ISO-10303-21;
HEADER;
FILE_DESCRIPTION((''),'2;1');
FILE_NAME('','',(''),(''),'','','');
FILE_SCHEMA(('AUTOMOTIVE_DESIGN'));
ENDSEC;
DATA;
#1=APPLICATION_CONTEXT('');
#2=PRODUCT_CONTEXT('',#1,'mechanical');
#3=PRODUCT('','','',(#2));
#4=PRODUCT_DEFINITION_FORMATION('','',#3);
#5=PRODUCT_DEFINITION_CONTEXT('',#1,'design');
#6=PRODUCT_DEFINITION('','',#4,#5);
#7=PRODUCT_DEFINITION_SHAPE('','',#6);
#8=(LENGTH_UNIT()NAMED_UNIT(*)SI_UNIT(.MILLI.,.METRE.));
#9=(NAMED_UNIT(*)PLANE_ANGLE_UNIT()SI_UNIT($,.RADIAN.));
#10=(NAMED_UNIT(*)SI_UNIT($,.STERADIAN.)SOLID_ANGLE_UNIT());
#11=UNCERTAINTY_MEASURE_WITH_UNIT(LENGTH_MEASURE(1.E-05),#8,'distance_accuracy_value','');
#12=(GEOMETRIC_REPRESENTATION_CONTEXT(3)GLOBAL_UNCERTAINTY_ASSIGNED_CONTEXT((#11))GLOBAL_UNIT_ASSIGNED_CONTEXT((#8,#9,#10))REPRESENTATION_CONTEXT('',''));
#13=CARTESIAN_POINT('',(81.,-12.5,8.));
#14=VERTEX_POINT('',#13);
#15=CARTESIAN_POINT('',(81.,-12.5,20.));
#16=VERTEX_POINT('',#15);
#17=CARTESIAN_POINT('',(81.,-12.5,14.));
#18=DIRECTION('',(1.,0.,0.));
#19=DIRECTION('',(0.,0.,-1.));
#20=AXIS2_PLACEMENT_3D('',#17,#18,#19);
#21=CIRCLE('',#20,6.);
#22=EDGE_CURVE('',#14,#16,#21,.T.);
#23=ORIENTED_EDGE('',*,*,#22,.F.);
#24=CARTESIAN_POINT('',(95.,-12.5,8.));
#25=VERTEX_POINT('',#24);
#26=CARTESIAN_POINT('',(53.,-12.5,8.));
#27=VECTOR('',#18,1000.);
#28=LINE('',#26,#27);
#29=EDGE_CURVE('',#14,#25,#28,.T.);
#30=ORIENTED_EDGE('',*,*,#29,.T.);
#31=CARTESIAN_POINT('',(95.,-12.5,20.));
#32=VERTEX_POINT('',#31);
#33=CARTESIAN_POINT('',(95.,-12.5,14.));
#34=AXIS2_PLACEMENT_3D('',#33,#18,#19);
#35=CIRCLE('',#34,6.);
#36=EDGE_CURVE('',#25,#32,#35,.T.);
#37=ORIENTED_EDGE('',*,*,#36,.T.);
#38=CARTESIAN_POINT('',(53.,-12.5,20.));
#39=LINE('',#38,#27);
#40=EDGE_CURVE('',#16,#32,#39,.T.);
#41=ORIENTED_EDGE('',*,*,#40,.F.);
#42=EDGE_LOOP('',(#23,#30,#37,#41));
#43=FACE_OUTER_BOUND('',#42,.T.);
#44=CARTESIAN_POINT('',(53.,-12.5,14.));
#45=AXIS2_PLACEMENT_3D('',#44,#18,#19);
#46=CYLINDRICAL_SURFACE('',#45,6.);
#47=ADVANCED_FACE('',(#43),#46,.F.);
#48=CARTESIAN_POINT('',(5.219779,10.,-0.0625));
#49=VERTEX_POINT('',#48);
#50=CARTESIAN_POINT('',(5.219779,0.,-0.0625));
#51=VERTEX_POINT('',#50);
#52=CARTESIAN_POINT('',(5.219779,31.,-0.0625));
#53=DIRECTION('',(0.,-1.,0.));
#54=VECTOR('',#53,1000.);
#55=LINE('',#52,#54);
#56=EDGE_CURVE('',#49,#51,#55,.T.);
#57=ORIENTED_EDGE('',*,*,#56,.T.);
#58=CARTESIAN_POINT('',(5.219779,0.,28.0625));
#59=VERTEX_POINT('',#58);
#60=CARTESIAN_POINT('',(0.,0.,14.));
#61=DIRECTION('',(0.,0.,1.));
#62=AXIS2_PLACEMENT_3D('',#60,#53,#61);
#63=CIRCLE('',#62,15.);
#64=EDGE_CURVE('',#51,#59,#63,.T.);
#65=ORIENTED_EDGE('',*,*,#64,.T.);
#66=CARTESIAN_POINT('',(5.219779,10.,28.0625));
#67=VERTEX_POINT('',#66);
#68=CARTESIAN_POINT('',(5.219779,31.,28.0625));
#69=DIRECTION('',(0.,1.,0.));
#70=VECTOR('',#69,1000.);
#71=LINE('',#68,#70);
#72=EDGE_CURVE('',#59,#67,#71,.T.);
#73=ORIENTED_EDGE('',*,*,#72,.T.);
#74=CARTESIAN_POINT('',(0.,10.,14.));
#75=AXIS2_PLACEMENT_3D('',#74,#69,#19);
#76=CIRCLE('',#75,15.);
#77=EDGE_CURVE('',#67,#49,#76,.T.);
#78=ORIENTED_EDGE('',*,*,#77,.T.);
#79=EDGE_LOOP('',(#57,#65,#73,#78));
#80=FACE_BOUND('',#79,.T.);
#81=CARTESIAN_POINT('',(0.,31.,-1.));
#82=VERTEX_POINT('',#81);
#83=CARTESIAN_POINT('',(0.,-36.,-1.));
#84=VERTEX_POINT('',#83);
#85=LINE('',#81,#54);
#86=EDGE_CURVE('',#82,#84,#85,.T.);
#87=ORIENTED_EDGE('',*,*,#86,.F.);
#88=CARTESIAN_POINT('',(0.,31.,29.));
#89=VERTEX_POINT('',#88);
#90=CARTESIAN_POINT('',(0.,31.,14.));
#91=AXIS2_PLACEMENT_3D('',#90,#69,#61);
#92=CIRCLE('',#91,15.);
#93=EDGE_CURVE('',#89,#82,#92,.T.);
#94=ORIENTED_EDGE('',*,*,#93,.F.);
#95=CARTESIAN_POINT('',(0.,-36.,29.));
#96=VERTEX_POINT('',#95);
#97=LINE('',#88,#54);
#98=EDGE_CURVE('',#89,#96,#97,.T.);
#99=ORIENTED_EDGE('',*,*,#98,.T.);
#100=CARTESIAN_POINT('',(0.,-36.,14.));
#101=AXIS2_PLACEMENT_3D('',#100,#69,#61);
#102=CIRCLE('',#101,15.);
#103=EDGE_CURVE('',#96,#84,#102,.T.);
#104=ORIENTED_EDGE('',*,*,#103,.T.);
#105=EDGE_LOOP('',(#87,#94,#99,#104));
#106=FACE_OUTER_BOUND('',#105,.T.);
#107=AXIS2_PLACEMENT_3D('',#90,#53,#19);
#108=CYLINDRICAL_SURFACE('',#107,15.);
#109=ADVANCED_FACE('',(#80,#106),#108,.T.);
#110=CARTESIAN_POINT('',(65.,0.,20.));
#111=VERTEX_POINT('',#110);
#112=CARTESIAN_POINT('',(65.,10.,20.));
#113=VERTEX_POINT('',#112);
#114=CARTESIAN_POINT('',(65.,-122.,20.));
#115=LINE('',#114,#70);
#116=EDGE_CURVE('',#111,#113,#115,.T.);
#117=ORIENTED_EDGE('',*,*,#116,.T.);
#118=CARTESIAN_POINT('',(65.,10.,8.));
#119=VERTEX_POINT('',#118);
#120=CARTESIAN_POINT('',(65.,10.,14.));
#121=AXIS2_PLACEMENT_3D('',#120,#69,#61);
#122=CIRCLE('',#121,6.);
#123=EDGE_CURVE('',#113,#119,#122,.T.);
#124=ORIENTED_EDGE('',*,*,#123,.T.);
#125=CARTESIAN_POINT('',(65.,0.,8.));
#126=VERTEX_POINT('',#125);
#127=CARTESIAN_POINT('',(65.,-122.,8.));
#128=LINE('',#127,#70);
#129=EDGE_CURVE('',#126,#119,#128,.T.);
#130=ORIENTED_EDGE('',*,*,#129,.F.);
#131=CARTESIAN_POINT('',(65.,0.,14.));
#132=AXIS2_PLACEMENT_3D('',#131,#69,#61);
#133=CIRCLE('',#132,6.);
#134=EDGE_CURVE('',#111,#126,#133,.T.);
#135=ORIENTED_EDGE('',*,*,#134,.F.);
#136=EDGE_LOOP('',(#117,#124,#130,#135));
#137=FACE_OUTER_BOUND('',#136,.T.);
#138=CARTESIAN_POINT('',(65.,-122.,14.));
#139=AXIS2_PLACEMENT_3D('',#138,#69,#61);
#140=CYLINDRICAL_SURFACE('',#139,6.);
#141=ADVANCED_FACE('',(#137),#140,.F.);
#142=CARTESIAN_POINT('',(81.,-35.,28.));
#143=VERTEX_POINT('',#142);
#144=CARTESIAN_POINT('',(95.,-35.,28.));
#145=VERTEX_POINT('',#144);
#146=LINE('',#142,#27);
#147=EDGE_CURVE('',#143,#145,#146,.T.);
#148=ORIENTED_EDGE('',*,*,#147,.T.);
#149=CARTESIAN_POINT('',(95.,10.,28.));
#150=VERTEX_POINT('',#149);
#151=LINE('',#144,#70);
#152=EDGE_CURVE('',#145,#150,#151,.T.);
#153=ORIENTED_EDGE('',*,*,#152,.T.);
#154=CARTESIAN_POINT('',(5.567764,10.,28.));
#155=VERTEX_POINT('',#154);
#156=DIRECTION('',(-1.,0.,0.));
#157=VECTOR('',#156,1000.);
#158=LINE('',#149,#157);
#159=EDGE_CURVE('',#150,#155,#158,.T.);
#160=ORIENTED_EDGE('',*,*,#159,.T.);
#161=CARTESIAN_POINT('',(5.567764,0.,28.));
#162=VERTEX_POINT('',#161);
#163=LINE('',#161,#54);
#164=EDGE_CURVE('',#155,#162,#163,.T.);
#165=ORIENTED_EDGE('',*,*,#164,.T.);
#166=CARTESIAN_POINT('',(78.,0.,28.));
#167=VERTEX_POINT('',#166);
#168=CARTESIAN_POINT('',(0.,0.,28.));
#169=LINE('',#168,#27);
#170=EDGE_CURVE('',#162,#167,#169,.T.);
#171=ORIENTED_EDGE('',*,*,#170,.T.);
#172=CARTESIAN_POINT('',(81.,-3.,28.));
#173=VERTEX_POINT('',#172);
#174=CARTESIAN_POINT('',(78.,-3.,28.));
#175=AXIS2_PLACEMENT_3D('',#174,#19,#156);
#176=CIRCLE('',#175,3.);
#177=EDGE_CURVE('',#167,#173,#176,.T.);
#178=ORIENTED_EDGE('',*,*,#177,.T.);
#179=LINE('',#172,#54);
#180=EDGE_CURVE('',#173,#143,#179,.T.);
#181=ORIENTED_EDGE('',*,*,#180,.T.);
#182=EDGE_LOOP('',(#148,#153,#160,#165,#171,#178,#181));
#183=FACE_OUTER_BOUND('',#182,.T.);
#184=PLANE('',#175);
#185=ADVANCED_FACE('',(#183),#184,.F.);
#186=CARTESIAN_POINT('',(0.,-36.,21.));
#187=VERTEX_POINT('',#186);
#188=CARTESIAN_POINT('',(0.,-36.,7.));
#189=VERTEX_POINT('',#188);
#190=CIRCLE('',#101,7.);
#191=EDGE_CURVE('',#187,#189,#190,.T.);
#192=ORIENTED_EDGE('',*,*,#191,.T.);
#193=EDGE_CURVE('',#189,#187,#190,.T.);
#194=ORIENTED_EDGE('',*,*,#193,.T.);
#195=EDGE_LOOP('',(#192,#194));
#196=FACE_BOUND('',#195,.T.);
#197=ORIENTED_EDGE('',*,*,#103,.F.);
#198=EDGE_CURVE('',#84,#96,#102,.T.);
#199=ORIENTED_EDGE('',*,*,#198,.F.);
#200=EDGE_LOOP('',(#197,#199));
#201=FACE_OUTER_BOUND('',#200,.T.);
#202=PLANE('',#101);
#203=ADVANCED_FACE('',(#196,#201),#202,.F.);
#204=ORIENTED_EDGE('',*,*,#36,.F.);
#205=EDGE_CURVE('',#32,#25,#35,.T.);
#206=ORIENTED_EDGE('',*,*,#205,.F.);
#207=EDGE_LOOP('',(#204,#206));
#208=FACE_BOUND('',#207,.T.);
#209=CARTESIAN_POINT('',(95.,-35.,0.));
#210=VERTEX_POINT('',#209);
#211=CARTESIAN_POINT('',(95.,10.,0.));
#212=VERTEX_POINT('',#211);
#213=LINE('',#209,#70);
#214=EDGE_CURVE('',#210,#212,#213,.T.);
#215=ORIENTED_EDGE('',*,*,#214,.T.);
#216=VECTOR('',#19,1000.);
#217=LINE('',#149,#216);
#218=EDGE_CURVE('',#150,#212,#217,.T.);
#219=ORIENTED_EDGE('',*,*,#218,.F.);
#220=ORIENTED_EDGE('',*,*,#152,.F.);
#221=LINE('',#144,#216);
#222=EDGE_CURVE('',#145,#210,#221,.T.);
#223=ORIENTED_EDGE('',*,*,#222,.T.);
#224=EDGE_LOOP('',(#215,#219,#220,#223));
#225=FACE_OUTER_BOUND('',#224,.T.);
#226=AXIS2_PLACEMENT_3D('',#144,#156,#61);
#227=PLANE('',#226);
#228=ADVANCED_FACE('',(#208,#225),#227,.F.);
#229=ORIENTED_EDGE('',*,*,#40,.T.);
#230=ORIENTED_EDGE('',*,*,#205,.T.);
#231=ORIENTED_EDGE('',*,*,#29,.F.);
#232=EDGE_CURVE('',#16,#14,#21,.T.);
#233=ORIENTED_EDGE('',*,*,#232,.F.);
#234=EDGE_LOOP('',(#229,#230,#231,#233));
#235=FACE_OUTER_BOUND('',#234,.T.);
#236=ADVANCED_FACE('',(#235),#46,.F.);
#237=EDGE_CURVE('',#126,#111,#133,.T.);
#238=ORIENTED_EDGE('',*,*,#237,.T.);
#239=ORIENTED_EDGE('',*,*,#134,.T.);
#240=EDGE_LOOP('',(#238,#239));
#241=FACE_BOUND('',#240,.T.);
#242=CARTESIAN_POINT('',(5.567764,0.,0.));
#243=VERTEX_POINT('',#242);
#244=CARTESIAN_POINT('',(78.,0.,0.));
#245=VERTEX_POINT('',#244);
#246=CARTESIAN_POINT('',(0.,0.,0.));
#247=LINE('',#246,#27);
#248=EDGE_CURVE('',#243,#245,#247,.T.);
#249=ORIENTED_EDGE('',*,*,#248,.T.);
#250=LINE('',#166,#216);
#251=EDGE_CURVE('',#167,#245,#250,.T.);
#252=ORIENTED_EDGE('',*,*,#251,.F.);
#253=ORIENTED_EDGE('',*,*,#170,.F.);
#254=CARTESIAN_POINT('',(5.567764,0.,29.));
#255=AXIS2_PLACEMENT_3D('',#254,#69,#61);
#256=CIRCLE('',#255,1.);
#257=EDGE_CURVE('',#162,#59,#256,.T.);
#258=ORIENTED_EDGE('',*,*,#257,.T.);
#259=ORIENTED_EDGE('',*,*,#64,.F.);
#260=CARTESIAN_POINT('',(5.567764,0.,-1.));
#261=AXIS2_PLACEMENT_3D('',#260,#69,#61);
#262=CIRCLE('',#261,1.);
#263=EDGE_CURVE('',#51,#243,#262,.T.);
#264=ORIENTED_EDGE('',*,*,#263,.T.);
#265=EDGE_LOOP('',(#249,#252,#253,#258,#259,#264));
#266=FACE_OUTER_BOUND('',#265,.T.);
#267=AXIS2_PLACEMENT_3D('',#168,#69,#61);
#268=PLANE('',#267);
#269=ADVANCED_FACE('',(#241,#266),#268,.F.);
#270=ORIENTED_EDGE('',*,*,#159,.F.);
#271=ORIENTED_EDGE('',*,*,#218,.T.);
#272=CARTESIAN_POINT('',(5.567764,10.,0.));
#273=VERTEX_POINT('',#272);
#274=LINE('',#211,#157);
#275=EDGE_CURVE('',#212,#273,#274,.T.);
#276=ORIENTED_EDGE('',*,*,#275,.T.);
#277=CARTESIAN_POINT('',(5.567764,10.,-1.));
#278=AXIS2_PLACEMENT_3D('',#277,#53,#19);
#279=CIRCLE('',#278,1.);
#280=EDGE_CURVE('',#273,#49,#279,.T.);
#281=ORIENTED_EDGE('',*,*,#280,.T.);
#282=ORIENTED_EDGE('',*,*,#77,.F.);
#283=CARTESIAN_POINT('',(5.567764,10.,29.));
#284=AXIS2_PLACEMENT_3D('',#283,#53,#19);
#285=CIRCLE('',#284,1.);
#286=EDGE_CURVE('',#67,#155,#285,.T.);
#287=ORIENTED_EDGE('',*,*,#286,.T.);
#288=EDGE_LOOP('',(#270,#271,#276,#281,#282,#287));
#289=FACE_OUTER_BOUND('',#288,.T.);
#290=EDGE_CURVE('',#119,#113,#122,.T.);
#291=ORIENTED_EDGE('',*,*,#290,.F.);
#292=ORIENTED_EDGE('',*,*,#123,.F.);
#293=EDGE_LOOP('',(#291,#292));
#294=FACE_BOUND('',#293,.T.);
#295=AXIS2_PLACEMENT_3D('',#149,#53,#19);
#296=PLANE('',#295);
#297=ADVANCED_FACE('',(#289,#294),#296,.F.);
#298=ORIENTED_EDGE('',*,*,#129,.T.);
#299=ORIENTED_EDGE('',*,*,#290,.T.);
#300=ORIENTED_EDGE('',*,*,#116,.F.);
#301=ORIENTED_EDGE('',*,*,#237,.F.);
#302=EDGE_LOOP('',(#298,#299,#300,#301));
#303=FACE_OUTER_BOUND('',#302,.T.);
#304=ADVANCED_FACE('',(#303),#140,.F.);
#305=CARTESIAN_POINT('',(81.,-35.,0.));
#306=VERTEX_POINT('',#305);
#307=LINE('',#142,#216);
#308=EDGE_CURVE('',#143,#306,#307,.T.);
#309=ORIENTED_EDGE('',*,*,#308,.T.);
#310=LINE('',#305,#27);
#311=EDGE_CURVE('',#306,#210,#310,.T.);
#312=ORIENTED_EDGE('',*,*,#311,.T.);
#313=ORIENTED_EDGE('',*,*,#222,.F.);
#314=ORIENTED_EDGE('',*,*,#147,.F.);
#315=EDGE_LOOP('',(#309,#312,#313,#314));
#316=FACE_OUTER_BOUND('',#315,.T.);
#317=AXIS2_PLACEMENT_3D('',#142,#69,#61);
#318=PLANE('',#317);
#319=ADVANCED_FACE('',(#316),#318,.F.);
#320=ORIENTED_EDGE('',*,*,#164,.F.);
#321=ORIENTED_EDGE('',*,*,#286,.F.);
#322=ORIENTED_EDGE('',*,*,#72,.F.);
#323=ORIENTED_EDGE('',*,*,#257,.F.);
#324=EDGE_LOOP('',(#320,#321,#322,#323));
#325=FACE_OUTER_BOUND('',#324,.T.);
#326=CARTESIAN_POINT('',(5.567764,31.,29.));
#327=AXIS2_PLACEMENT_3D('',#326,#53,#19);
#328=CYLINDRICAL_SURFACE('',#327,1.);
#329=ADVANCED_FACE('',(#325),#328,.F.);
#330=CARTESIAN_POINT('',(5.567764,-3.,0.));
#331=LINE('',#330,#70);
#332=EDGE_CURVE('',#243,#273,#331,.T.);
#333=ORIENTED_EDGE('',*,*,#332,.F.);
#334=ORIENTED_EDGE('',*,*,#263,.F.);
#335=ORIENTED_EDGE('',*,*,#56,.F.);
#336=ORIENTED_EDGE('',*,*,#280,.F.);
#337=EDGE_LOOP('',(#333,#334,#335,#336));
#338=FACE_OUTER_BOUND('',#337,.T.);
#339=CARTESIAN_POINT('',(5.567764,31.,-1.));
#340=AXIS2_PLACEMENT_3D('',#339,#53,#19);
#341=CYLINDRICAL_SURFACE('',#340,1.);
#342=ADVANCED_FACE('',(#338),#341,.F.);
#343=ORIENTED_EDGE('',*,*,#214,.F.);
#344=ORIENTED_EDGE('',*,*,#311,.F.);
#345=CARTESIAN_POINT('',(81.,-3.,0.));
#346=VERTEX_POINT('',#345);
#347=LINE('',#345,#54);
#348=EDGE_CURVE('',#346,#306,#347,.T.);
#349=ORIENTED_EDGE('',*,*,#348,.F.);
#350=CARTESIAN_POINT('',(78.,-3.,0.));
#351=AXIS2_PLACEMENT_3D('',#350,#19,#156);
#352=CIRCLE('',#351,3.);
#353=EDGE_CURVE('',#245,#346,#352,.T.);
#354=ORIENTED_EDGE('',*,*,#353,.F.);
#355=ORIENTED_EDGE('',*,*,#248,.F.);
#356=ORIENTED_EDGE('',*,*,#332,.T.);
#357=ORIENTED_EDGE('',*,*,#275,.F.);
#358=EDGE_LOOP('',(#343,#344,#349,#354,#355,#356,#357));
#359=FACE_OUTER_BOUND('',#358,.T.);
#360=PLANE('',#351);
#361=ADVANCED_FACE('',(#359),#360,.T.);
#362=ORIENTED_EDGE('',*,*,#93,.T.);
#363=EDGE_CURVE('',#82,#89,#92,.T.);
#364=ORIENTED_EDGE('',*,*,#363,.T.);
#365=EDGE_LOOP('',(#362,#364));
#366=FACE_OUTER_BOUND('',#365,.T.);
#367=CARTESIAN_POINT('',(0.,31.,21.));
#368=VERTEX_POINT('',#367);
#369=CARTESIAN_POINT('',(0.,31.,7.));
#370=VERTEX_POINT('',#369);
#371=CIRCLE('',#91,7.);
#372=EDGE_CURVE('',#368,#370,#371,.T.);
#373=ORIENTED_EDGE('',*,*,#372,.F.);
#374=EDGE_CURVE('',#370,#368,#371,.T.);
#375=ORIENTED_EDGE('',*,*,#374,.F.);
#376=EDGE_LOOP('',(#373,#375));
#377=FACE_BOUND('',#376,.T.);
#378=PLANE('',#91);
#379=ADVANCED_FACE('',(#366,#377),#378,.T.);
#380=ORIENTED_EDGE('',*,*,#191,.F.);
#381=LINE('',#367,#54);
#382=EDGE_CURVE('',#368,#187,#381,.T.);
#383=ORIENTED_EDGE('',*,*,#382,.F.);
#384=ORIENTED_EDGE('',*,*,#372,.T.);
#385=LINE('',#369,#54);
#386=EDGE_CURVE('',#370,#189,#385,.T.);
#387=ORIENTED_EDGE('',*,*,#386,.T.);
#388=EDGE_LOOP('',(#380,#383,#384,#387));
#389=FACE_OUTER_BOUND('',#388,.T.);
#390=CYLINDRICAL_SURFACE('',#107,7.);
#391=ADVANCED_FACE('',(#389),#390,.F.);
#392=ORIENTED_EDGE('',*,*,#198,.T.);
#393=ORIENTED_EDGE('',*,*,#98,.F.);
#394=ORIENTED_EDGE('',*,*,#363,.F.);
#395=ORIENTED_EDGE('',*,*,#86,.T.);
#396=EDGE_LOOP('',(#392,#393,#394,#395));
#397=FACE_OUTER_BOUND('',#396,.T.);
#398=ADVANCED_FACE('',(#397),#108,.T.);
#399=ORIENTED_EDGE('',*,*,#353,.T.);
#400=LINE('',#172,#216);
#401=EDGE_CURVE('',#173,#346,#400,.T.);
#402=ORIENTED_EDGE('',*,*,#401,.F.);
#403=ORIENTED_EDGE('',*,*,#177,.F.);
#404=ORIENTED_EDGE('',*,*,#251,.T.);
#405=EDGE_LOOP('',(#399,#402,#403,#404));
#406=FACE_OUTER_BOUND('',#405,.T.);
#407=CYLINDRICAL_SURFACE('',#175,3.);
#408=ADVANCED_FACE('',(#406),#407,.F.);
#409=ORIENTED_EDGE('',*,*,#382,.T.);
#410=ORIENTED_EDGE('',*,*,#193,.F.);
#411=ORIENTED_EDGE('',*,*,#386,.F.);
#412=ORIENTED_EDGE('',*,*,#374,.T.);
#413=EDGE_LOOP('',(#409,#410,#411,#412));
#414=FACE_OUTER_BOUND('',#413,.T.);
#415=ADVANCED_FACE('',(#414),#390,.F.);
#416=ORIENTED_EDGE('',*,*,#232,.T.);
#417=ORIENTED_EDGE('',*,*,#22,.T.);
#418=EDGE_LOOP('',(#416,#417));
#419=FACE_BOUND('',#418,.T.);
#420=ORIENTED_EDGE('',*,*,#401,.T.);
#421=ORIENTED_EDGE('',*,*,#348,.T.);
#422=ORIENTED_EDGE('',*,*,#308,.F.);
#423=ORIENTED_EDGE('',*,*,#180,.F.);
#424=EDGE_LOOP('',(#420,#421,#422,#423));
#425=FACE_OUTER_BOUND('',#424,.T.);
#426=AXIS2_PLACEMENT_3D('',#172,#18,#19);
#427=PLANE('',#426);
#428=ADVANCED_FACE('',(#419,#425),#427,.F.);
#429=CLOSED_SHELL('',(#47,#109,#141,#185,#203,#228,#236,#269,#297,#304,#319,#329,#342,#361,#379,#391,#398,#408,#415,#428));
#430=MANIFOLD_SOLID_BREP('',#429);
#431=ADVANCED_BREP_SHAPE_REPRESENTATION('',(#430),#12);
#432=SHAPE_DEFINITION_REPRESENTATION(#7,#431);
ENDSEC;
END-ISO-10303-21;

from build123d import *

# Parameters (mm, degrees)
CRANK_ARM_DEPTH        = 28
PIVOT_HUB_DEPTH        = 21
PIVOT_HUB_DEPTH_BACK   = 46
PIVOT_HUB_SKETCH_R     = 15
PIVOT_HUB_SKETCH_R_2   = 7
HUB_FILLET_R1_R        = 1
TOP_START              = 132
TOP_THROUGH_HOLE_DEPTH = 132
ARM_HOLE_SKETCH_R      = 6
ARM_THROUGH_HOLE_DEPTH = 132
BORE_SKETCH_R          = 6
THROUGH_BORE_DEPTH     = 42


with BuildPart() as part:
    # Arm Profile Sketch → Crank Arm (new body)
    with BuildSketch(Plane.XY):
        with BuildLine():
            Line((0, 0), (78, 0))
            ThreePointArc((78, 0), (80.121320344, -0.878679656), (81, -3))
            Line((81, -3), (81, -35))
            Line((81, -35), (95, -35))
            Line((95, -35), (95, 10))
            Line((95, 10), (0, 10))
            Line((0, 10), (0, 0))
        make_face()
    extrude(amount=CRANK_ARM_DEPTH)

    # Pivot Hub Sketch → Pivot Hub (add, two sides: drawn at the far end of the back side and taken through both)
    with BuildSketch(Plane(origin=(0, 10, 0), x_dir=(1, 0, 0), z_dir=(0, 1, 0)).offset(-PIVOT_HUB_DEPTH_BACK)):
        with Locations(Location((0, -14, 0), (0, 0, 270))):
            Circle(PIVOT_HUB_SKETCH_R)
        with Locations(Location((0, -14, 0), (0, 0, 270))):
            Circle(PIVOT_HUB_SKETCH_R_2, mode=Mode.SUBTRACT)
    extrude(amount=PIVOT_HUB_DEPTH + PIVOT_HUB_DEPTH_BACK)

    # Hub Fillet R1
    hub_fillet_r1_edges = [part.edges().sort_by_distance(p)[0] for p in [
        (5.385164807, 5, 0),
        (5.385164807, 5, 28),
    ]]
    fillet(hub_fillet_r1_edges, radius=HUB_FILLET_R1_R)

    # Top Hole Sketch → Top Through Hole (cut)
    with BuildSketch(Plane(origin=(0, 0, 0), x_dir=(1, 0, 0), z_dir=(0, 1, 0)).offset(TOP_START)):
        with BuildLine():
            Line((0, -7), (0, -21))
            ThreePointArc((0, -21), (7, -14), (0, -7))
        make_face()
    extrude(amount=-TOP_THROUGH_HOLE_DEPTH, mode=Mode.SUBTRACT)

    # Arm Hole Sketch → Arm Through Hole (cut)
    with BuildSketch(Plane(origin=(0, 10, 0), x_dir=(1, 0, 0), z_dir=(0, 1, 0))):
        with Locations(Location((65, -14, 0), (0, 0, 270))):
            Circle(ARM_HOLE_SKETCH_R)
    extrude(amount=-ARM_THROUGH_HOLE_DEPTH, mode=Mode.SUBTRACT)

    # Bore Sketch → Through Bore (cut)
    with BuildSketch(Plane(origin=(95, 0, 0), x_dir=(0, 0, -1), z_dir=(1, 0, 0))):
        with Locations((-14, -12.5)):
            Circle(BORE_SKETCH_R)
    extrude(amount=-THROUGH_BORE_DEPTH, mode=Mode.SUBTRACT)


solid = part.part
